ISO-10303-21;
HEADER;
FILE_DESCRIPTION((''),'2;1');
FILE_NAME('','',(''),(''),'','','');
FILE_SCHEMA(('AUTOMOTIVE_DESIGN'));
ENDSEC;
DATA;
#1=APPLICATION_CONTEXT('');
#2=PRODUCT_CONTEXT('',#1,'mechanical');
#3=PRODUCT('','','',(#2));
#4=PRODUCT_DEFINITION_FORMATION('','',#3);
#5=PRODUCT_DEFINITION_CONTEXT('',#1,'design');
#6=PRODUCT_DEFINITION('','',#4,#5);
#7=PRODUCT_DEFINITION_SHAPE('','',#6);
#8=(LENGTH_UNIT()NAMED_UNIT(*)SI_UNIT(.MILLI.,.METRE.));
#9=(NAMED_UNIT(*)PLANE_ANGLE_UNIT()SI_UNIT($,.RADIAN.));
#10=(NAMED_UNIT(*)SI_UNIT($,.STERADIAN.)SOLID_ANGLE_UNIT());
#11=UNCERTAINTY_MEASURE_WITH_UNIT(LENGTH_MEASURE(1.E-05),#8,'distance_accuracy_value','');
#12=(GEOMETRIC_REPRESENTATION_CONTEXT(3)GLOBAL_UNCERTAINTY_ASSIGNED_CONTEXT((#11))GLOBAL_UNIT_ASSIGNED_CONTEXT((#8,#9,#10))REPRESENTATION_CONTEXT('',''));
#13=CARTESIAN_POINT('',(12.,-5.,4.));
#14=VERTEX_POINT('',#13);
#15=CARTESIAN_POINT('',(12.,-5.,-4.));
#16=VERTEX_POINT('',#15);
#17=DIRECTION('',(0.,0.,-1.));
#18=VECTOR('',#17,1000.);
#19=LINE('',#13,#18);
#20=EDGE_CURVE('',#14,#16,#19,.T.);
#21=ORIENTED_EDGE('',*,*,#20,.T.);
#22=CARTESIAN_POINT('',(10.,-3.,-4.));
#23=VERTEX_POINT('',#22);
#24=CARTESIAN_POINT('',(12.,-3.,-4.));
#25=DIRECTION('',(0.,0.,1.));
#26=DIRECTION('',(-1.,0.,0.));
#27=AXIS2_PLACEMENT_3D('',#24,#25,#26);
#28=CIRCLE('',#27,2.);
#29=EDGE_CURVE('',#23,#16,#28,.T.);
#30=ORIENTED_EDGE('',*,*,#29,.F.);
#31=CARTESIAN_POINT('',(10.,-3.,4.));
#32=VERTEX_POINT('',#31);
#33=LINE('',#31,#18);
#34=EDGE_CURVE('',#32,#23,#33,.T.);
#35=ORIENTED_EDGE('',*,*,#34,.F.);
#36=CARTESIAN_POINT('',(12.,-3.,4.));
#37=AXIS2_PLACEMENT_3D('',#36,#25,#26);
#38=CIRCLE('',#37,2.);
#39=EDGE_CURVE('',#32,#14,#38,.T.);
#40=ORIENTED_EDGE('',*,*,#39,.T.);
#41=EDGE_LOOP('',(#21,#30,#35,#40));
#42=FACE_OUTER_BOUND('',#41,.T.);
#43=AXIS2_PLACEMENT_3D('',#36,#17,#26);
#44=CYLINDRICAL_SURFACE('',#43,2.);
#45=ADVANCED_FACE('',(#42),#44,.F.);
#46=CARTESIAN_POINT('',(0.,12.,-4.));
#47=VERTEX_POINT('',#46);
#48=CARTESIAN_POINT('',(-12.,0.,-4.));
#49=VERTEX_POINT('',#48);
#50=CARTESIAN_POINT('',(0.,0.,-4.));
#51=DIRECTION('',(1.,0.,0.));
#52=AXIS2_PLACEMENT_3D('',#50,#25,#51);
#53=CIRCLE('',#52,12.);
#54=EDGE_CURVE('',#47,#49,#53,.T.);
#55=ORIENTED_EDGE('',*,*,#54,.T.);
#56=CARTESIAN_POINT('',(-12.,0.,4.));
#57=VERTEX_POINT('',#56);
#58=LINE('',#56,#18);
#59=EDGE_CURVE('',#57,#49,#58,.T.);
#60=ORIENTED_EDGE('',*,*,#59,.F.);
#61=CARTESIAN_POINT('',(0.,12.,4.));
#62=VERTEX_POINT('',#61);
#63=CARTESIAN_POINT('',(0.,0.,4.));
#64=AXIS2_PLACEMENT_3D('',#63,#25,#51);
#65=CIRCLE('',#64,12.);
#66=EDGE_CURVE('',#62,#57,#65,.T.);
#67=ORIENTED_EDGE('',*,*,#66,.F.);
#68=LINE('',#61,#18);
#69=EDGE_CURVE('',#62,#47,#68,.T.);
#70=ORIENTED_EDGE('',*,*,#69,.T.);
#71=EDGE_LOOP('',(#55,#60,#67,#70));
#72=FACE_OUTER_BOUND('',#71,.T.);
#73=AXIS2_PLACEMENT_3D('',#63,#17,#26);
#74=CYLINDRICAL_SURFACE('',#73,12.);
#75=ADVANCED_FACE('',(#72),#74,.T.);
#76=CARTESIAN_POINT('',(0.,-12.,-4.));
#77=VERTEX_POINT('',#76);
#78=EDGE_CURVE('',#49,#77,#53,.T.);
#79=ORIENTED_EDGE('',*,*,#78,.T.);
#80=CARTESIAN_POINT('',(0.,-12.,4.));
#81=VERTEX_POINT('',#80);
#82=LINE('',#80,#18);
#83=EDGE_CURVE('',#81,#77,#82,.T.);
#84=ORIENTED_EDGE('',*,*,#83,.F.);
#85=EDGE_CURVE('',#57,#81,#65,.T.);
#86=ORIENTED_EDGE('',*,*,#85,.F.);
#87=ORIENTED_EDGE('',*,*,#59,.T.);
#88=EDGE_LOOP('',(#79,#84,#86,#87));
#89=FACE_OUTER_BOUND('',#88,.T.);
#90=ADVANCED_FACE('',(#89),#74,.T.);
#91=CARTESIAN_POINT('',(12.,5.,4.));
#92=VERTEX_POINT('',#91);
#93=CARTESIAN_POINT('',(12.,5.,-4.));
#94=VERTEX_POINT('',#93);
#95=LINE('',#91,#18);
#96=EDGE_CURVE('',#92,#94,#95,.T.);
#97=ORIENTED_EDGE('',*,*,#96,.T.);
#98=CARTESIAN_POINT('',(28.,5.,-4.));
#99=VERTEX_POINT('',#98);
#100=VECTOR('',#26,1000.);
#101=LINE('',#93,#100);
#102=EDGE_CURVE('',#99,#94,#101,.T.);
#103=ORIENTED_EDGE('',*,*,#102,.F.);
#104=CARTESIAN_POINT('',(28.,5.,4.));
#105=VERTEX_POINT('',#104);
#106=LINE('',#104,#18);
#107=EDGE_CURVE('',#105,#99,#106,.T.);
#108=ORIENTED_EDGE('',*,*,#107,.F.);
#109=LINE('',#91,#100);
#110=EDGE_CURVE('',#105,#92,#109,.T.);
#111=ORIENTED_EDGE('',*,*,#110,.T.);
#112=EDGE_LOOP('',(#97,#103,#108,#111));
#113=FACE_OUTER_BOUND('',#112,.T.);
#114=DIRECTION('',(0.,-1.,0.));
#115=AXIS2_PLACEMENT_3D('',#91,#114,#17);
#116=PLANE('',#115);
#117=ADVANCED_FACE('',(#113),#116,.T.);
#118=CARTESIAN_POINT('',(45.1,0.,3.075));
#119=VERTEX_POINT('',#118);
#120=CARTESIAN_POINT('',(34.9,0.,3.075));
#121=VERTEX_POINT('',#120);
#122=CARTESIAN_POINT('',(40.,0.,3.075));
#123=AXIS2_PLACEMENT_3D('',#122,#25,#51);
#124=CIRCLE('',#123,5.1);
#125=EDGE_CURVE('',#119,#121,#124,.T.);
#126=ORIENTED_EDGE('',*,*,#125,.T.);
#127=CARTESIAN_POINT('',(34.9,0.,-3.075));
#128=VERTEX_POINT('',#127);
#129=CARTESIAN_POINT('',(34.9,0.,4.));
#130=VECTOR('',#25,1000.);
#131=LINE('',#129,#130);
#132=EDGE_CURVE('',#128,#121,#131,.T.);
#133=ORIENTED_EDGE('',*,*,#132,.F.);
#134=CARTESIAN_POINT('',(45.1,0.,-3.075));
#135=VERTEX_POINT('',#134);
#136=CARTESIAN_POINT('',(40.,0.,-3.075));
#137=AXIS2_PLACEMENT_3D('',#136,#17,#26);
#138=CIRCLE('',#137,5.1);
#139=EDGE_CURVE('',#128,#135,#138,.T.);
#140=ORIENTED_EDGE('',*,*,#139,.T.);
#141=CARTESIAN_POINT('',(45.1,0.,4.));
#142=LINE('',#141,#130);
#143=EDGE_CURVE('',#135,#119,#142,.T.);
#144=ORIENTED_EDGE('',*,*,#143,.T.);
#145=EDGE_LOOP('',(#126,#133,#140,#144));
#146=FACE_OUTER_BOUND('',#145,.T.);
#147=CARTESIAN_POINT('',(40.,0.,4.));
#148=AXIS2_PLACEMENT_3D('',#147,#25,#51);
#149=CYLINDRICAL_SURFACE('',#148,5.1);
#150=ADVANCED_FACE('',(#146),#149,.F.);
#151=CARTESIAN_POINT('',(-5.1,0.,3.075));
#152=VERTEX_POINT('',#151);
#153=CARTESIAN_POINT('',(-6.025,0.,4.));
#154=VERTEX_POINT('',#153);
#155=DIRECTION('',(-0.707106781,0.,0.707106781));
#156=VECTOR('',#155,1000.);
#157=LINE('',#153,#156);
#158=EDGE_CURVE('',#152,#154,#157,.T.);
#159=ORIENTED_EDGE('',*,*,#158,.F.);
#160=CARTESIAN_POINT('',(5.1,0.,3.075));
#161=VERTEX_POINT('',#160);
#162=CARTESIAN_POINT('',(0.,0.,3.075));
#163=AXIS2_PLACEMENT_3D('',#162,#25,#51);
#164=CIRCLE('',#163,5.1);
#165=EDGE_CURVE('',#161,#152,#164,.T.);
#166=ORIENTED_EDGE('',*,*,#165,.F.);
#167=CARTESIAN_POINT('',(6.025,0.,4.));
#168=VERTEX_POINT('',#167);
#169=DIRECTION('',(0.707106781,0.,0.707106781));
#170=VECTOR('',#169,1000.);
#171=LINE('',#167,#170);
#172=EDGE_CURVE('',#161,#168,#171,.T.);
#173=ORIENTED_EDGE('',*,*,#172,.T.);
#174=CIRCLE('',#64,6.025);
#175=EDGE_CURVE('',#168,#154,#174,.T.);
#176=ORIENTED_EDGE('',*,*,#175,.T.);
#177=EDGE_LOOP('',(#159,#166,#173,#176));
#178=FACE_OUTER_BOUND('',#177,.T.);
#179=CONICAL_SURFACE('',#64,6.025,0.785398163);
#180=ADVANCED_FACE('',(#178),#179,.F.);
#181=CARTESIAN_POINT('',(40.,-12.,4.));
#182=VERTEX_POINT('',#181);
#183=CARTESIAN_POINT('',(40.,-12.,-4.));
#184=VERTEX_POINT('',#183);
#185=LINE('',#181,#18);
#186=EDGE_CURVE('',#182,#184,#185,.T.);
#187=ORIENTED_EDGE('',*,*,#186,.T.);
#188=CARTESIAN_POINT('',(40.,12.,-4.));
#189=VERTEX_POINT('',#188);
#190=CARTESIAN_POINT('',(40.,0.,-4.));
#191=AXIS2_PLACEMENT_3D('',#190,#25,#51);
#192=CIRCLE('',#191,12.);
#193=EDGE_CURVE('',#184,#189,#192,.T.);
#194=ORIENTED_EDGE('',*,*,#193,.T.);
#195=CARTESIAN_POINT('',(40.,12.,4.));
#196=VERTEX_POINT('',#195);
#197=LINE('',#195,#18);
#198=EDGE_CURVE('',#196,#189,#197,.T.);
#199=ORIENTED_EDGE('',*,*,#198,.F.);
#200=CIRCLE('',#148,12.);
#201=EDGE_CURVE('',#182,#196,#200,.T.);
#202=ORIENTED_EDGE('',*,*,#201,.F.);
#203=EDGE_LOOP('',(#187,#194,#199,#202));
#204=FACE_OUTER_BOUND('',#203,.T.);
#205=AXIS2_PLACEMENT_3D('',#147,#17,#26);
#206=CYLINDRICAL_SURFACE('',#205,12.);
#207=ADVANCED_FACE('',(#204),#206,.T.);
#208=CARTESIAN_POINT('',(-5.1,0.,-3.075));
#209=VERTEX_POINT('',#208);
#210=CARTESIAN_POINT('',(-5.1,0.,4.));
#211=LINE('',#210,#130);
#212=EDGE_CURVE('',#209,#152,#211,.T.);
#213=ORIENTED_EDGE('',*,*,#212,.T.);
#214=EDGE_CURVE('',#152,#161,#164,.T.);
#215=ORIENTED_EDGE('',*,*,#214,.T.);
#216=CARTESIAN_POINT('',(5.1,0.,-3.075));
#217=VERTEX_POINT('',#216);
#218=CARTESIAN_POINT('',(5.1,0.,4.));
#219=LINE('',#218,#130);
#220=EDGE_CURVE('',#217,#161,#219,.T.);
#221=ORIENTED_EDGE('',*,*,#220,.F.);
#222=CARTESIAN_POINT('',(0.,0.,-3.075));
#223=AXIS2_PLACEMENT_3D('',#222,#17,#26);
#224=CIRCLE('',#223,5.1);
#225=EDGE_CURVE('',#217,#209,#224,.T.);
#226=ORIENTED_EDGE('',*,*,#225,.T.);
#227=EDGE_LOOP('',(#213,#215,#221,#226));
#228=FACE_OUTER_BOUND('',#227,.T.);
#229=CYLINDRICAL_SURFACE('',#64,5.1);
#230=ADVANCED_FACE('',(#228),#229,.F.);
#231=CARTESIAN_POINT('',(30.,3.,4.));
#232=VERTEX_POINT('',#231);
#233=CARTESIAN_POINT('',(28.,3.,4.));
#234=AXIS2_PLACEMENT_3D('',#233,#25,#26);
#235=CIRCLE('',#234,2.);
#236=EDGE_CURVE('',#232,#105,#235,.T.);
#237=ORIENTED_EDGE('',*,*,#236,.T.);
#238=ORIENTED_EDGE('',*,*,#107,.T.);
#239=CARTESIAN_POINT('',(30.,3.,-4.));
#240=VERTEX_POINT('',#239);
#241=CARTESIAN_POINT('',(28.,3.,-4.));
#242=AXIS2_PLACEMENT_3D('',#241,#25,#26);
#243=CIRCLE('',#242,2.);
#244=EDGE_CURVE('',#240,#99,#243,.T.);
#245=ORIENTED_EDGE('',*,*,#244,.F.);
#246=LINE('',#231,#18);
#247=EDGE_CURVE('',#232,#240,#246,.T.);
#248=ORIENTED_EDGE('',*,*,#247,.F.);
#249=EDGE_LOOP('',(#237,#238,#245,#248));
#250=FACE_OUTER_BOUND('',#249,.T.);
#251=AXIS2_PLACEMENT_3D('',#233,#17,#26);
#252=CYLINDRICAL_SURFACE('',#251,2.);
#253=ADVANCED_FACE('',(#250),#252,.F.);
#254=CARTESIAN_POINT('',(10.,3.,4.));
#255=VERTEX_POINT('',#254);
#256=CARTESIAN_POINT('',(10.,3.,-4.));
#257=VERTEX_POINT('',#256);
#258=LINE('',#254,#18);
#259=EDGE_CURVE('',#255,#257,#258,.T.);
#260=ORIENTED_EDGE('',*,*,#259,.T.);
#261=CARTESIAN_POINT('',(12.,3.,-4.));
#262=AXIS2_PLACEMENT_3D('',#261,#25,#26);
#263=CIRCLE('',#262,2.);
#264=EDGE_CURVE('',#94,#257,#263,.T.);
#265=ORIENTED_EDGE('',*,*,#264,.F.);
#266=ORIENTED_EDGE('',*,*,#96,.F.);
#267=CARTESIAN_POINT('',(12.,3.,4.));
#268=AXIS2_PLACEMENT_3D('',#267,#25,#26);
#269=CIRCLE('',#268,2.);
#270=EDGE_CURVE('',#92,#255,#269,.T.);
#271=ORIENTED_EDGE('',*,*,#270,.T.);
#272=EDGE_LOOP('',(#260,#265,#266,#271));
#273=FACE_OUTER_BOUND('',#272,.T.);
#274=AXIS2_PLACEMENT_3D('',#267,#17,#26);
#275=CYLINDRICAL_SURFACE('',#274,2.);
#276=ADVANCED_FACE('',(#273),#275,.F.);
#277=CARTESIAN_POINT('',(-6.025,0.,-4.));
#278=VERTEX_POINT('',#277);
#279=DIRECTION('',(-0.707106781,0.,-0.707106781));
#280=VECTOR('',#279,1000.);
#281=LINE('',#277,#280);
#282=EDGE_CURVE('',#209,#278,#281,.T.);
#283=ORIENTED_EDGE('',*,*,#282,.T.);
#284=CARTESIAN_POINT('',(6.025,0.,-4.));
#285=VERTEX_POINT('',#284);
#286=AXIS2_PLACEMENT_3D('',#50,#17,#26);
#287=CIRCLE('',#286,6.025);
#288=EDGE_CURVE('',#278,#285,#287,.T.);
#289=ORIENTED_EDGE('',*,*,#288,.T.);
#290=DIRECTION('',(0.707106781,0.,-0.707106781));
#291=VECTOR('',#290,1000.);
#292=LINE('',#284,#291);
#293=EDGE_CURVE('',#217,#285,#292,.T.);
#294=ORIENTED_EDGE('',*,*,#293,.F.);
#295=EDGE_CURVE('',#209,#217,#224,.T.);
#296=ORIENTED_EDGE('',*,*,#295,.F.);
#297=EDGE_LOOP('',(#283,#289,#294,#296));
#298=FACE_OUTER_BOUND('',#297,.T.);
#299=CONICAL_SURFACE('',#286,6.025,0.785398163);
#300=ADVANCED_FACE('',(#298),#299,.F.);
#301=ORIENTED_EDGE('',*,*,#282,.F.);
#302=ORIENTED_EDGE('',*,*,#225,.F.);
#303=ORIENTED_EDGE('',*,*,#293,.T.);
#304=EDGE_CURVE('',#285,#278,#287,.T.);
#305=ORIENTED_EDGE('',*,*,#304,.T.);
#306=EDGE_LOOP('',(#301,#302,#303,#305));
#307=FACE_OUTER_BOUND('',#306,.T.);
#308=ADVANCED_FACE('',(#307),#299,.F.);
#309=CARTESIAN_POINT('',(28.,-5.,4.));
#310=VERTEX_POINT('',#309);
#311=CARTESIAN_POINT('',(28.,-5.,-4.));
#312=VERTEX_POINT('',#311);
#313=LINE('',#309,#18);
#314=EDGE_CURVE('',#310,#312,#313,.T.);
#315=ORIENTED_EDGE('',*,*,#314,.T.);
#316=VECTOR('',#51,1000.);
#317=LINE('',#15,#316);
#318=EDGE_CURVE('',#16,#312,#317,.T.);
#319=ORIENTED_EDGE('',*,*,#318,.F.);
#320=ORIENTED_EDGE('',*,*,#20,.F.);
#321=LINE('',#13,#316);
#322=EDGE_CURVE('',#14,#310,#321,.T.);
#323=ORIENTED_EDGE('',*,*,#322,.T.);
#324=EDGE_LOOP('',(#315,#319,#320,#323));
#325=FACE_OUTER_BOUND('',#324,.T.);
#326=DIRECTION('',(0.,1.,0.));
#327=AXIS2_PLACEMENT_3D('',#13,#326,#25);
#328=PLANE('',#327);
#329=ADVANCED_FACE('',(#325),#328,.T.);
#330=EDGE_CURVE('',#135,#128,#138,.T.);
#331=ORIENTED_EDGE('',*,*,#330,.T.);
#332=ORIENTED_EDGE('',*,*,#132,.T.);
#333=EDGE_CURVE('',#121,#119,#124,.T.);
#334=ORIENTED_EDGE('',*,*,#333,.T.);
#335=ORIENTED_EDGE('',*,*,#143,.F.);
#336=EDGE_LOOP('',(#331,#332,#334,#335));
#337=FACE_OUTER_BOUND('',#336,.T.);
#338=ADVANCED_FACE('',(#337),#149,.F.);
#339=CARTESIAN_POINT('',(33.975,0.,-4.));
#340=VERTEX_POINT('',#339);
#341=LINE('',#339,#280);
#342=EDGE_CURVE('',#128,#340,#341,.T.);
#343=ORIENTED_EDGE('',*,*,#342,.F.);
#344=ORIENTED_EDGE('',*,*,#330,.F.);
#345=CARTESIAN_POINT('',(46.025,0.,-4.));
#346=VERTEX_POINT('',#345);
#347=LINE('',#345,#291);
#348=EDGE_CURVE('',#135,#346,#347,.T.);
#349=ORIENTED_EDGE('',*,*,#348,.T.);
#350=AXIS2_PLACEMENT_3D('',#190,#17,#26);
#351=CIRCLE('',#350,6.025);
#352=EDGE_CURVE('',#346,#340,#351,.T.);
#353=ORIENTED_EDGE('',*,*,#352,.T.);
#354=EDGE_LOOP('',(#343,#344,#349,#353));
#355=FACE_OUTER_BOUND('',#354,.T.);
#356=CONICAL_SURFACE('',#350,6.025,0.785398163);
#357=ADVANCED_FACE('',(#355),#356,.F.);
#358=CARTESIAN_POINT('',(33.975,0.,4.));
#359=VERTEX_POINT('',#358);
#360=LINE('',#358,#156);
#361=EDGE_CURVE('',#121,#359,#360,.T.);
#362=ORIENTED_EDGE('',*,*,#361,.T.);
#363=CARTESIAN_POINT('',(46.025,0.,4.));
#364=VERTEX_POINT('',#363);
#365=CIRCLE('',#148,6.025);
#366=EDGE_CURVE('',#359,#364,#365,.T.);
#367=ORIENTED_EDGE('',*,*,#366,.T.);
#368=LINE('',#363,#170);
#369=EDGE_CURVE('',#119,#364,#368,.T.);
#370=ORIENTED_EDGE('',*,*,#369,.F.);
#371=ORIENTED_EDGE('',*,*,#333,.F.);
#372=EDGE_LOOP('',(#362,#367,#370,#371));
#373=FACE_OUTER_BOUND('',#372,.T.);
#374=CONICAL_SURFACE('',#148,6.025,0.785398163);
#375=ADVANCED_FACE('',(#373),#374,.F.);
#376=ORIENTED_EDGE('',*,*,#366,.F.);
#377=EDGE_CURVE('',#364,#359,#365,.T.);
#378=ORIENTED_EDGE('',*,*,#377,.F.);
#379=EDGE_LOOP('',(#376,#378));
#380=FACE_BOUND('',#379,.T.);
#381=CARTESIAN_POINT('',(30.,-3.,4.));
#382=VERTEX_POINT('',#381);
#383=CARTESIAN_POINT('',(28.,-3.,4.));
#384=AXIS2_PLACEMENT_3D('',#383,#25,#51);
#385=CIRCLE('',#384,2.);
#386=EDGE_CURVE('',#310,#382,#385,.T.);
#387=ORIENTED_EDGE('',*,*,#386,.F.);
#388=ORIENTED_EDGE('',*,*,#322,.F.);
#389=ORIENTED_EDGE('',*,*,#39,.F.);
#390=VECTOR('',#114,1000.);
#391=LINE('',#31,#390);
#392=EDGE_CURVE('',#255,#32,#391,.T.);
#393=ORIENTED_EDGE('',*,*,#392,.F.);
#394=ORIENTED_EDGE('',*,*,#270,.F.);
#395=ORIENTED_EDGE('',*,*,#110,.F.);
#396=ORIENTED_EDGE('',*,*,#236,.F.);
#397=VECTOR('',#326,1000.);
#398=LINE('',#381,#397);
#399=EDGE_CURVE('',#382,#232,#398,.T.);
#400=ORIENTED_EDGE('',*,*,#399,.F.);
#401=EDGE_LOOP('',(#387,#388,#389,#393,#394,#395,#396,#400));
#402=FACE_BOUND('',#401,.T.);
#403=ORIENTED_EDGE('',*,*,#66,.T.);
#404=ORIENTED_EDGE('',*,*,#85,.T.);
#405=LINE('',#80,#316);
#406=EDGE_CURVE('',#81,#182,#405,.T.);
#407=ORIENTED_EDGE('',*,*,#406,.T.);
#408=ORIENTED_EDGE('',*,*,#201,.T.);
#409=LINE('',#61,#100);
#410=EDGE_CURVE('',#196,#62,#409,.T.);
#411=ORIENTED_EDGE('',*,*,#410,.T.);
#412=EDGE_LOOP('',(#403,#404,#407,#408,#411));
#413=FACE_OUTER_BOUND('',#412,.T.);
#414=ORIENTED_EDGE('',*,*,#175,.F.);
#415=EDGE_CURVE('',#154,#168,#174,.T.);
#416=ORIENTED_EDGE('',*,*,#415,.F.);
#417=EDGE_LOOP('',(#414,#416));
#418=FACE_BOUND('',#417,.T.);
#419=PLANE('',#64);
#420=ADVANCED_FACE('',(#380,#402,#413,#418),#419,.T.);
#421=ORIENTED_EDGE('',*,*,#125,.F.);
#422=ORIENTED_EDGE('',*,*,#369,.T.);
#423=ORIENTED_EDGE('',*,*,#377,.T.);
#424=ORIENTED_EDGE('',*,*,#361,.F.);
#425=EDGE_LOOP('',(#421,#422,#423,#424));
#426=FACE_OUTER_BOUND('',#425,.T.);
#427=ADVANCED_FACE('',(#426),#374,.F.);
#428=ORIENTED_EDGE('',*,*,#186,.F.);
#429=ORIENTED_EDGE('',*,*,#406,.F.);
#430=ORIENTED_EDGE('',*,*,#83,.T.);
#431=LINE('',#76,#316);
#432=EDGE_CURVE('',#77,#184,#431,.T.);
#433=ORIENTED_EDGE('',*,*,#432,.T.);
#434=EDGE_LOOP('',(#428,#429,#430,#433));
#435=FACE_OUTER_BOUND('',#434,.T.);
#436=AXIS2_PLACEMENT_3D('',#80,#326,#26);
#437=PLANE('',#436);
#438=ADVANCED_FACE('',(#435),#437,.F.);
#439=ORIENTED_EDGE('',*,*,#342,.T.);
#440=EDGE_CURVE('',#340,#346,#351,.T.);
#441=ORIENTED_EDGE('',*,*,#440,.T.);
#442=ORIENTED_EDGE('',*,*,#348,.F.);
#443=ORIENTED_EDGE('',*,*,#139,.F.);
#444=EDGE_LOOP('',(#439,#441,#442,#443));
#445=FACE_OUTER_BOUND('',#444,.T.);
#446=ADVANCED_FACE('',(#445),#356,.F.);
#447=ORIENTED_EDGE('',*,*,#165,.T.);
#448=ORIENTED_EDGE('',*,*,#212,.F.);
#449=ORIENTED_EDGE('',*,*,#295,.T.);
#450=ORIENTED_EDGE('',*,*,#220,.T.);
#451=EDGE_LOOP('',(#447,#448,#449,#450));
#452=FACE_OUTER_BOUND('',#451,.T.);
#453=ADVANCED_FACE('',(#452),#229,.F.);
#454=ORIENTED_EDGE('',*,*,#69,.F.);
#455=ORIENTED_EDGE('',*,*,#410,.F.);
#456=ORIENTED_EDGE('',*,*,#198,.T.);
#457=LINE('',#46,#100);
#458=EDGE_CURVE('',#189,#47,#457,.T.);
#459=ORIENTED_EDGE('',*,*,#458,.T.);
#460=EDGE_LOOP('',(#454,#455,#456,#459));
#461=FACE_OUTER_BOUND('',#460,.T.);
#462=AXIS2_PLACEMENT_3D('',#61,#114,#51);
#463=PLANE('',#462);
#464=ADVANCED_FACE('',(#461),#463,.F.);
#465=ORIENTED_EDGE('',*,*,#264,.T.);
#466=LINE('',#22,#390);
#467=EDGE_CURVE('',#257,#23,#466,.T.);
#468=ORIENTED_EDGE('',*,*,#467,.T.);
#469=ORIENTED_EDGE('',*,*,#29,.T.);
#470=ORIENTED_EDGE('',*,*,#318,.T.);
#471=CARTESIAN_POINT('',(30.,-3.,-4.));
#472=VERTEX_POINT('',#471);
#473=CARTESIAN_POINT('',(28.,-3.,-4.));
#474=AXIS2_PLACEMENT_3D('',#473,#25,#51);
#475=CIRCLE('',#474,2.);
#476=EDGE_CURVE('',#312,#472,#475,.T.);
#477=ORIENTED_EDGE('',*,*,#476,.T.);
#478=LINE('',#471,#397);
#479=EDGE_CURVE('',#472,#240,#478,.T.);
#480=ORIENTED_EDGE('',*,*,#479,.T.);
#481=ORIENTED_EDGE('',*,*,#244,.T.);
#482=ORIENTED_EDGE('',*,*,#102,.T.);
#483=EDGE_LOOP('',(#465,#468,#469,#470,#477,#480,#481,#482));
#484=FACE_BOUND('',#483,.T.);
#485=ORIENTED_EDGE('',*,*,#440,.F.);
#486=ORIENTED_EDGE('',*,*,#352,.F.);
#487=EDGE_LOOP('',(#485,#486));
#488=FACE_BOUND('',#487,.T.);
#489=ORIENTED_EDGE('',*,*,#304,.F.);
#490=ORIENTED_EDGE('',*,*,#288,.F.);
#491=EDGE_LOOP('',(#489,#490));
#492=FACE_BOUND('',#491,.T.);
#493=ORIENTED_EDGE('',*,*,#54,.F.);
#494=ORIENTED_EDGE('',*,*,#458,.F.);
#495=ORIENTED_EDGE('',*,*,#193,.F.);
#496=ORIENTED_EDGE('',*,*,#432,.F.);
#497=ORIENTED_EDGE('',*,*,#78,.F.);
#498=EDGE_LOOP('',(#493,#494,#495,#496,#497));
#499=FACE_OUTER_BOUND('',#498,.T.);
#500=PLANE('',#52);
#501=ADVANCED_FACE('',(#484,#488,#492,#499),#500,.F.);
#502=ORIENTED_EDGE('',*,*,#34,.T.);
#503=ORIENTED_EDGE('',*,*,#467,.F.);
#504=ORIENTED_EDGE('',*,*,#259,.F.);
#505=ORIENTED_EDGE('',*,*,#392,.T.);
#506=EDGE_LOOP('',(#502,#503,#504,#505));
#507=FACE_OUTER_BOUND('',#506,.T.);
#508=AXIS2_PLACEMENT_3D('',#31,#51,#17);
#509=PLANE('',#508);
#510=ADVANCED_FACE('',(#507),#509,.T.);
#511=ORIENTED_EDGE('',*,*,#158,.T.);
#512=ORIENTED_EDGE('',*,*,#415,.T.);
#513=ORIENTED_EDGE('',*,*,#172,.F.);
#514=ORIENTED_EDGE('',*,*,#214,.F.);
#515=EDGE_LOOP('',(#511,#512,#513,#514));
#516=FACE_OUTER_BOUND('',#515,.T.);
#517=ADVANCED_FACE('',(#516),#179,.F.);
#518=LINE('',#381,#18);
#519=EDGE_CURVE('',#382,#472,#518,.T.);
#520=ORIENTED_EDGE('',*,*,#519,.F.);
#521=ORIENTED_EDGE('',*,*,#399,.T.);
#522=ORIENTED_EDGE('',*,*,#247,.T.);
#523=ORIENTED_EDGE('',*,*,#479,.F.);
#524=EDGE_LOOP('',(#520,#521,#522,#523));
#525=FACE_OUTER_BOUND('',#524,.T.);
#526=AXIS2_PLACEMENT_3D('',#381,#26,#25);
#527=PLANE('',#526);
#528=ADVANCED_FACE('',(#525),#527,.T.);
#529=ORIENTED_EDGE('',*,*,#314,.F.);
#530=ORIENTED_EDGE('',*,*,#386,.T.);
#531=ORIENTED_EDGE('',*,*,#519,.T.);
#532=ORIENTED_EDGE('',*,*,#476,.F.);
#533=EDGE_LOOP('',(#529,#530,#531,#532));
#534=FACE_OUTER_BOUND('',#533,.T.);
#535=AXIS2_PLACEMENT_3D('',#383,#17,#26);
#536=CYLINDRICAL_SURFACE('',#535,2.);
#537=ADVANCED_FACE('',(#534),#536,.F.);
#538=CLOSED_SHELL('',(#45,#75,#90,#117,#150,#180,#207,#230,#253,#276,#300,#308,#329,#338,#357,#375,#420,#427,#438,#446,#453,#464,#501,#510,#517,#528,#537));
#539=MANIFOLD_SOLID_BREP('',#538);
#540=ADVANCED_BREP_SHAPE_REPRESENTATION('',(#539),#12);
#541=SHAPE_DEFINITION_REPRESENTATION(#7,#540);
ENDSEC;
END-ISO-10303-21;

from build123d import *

# Parameters (mm, degrees)
BOSS_EXTRUDE1_DEPTH = 4


with BuildPart() as part:
    # Sketch1 → Boss-Extrude1 (new, symmetric)
    with BuildSketch(Plane.XY):
        with BuildLine():
            Line((0, 12), (40, 12))
            ThreePointArc((40, 12), (52, 0), (40, -12))
            Line((40, -12), (0, -12))
            ThreePointArc((0, -12), (-12, 0), (0, 12))
        make_face()
        with BuildLine():
            Line((12, -5), (28, -5))
            ThreePointArc((28, -5), (29.414213562, -4.414213562), (30, -3))
            Line((30, -3), (30, 3))
            ThreePointArc((30, 3), (29.414213562, 4.414213562), (28, 5))
            Line((28, 5), (12, 5))
            ThreePointArc((12, 5), (10.585786438, 4.414213562), (10, 3))
            Line((10, 3), (10, -3))
            ThreePointArc((10, -3), (10.585786438, -4.414213562), (12, -5))
        make_face(mode=Mode.SUBTRACT)
    extrude(amount=BOSS_EXTRUDE1_DEPTH, both=True)

    # Sketch2 → M12 Tapped Hole1 (revolve, cut)
    with BuildSketch(Plane(origin=(0, 0, 4), x_dir=(0, -1, 0), z_dir=(1, 0, 0))):
        Polygon((0, 0), (0, 32.75), (5.1, 29.685610843), (5.1, 0.925), (6.025, 0), align=None)
    m12_tapped_hole1 = revolve(axis=Axis((0, 0, 10.35), (0, 0, -1)), mode=Mode.SUBTRACT)

    # Mirror1: M12 Tapped Hole1 across plane
    add(m12_tapped_hole1.mirror(Plane.XY), mode=Mode.SUBTRACT)

    # Mirror2: M12 Tapped Hole1 across plane
    add(m12_tapped_hole1.mirror(Plane(origin=(20, 0, 0), x_dir=(0, 0, 1), z_dir=(1, 0, 0))), mode=Mode.SUBTRACT)

    # Mirror2 copy 1 sketch → Mirror2 copy 1 (revolve, cut)
    with BuildSketch(Plane(origin=(40, 0, -4), x_dir=(0, -1, 0), z_dir=(-1, 0, 0))):
        Polygon((0, 0), (0, 32.75), (5.1, 29.685610843), (5.1, 0.925), (6.025, 0), align=None)
    revolve(axis=Axis((40, 0, -10.35), (0, 0, 1)), mode=Mode.SUBTRACT)


solid = part.part
